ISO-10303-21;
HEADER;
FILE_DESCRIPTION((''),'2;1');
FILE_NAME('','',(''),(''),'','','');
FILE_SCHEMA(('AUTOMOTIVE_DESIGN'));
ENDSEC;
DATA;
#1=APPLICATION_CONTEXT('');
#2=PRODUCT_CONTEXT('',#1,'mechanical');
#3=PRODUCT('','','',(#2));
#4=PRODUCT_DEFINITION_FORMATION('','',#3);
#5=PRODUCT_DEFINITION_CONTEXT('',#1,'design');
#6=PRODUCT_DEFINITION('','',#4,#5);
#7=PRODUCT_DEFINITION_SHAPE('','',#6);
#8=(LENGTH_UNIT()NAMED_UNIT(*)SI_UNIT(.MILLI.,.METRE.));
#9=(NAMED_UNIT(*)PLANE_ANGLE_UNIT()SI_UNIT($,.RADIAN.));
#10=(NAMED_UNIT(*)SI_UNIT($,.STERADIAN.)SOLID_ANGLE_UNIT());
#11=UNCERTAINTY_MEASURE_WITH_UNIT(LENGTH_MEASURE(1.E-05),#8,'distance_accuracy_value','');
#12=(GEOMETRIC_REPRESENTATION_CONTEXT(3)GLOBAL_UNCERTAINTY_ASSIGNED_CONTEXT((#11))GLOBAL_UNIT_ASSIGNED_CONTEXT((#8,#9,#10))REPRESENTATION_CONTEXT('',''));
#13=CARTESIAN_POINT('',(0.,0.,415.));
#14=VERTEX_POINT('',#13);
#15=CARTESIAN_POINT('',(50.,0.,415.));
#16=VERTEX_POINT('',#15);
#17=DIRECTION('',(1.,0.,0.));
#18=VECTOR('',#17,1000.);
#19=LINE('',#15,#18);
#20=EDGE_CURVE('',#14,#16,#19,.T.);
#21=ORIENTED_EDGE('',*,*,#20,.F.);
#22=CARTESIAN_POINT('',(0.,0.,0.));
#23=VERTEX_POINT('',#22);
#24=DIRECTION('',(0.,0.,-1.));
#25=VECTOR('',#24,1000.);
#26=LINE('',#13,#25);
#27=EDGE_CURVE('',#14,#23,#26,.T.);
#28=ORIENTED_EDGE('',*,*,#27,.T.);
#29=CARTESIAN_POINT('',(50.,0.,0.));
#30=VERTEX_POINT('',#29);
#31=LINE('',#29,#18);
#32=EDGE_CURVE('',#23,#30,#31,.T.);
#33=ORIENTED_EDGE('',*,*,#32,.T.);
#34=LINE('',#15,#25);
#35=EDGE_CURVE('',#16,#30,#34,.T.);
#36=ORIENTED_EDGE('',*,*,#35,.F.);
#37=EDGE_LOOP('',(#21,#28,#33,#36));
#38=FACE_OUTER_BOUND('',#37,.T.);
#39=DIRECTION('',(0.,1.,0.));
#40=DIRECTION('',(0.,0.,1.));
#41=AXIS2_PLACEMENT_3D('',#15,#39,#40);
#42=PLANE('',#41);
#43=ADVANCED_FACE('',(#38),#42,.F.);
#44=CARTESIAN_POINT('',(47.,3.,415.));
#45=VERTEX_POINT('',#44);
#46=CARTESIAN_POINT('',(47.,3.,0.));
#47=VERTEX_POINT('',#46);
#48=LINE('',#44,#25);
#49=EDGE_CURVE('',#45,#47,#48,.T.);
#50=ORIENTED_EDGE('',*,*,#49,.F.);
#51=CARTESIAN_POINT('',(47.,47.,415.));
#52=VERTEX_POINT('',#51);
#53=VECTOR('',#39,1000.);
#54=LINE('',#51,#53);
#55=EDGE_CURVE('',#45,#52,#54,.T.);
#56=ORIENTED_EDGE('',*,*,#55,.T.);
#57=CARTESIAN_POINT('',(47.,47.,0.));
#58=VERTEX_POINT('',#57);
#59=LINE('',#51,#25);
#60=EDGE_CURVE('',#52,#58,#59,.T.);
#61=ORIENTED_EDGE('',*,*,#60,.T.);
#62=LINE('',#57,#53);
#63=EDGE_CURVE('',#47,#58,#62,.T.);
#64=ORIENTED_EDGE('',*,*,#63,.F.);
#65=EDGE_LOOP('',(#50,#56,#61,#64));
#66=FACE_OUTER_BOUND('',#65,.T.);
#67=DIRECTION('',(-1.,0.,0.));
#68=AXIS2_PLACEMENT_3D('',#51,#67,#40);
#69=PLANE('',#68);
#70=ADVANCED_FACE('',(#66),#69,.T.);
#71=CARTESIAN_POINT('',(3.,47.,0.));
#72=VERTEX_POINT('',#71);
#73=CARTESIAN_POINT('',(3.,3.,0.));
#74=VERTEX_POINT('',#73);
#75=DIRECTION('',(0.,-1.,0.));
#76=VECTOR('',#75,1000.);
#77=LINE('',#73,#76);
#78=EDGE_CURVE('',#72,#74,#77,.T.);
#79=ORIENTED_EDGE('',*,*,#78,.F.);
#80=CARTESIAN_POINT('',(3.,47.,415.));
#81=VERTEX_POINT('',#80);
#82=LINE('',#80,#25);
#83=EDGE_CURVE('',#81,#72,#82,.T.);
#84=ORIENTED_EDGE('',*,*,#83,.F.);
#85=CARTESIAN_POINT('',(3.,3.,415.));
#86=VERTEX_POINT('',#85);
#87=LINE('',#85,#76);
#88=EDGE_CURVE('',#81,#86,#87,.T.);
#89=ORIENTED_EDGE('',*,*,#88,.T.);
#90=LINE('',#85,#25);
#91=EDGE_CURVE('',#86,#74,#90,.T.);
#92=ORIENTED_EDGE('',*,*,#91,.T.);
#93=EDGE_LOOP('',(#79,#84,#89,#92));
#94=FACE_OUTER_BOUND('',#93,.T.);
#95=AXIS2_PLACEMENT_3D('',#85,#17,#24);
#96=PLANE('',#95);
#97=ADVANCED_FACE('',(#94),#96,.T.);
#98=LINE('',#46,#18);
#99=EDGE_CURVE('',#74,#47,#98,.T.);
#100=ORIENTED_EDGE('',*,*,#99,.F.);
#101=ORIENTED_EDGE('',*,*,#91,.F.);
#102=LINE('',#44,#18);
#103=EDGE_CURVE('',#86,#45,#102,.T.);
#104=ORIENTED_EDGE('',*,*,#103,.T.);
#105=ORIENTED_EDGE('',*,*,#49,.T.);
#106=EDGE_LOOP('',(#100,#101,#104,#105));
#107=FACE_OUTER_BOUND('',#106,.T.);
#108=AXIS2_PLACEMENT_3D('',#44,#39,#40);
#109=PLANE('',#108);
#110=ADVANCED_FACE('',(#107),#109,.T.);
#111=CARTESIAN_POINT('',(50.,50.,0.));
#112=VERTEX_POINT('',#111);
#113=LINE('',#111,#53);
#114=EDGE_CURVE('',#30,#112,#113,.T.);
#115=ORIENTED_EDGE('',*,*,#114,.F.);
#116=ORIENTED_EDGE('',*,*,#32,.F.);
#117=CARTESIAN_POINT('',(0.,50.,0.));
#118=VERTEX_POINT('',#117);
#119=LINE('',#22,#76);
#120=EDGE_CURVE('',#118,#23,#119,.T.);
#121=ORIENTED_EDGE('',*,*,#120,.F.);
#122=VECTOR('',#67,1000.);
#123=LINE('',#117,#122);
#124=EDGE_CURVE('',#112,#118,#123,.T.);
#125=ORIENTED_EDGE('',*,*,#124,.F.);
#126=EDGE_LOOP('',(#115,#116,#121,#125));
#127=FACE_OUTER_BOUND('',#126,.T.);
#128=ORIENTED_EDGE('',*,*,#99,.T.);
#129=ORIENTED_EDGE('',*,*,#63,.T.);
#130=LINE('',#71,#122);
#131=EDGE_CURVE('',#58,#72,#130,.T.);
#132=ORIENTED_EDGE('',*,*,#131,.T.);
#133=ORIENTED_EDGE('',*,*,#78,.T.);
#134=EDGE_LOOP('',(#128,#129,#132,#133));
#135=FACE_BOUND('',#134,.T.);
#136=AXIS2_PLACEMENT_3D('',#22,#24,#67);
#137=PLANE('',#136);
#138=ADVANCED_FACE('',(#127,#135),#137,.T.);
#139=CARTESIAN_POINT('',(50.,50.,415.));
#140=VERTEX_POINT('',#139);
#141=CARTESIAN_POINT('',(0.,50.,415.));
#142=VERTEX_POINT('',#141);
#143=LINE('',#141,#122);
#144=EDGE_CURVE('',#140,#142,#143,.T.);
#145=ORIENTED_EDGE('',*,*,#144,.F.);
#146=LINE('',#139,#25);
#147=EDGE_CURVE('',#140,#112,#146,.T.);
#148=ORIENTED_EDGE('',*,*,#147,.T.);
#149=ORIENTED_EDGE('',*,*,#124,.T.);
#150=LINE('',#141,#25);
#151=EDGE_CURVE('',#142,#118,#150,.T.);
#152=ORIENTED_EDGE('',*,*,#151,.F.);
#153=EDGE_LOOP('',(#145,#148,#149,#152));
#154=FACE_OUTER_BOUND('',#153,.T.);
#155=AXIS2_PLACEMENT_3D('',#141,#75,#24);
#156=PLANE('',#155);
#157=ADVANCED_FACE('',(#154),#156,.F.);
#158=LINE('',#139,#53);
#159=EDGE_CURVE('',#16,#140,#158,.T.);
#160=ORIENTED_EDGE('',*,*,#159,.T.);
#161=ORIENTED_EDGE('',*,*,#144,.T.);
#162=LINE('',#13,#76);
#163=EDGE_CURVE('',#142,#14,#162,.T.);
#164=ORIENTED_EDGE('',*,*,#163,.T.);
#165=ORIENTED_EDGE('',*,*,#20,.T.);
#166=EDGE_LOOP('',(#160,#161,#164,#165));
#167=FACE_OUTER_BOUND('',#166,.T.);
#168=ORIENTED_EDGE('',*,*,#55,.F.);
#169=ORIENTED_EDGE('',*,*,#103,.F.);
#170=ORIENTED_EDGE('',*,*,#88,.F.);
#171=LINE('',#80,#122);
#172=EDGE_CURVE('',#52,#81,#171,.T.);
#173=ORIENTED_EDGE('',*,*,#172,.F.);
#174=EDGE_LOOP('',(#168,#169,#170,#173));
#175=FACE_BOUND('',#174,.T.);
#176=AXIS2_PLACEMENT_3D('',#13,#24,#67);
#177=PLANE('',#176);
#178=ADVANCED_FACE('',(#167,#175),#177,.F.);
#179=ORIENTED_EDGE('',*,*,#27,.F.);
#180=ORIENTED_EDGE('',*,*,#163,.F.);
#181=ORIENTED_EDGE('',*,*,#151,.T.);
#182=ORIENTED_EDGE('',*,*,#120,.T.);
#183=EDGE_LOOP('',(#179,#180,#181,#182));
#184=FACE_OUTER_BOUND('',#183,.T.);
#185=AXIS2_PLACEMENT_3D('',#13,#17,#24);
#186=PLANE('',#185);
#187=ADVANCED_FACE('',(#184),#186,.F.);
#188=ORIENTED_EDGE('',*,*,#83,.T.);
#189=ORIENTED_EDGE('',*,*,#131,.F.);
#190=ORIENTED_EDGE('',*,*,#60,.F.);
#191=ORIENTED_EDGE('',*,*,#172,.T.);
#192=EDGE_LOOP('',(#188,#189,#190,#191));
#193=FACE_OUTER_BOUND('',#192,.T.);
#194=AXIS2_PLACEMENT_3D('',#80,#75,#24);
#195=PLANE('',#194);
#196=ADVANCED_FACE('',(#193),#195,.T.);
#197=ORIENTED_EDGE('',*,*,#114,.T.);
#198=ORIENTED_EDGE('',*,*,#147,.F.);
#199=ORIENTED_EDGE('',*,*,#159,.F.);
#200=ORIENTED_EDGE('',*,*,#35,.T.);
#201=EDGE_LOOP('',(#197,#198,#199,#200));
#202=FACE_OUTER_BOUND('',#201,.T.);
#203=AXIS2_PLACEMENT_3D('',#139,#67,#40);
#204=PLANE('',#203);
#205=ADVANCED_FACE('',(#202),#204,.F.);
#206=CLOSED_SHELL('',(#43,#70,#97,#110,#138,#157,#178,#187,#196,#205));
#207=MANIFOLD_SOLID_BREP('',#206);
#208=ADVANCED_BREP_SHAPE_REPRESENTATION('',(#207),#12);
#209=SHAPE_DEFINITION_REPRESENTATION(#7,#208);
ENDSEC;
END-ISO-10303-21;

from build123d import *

# Parameters (mm, degrees)
SKETCH_1_W      = 50
SKETCH_1_H      = 50
SKETCH_1_W_2    = 44
SKETCH_1_H_2    = 44
EXTRUDE_1_DEPTH = 415


with BuildPart() as part:
    # 草图1 → 凸台-拉伸1 (new body)
    with BuildSketch(Plane.XY):
        with Locations((25, 25)):
            Rectangle(SKETCH_1_W, SKETCH_1_H)
        with Locations((25, 25)):
            Rectangle(SKETCH_1_W_2, SKETCH_1_H_2, mode=Mode.SUBTRACT)
    extrude(amount=EXTRUDE_1_DEPTH)


solid = part.part
